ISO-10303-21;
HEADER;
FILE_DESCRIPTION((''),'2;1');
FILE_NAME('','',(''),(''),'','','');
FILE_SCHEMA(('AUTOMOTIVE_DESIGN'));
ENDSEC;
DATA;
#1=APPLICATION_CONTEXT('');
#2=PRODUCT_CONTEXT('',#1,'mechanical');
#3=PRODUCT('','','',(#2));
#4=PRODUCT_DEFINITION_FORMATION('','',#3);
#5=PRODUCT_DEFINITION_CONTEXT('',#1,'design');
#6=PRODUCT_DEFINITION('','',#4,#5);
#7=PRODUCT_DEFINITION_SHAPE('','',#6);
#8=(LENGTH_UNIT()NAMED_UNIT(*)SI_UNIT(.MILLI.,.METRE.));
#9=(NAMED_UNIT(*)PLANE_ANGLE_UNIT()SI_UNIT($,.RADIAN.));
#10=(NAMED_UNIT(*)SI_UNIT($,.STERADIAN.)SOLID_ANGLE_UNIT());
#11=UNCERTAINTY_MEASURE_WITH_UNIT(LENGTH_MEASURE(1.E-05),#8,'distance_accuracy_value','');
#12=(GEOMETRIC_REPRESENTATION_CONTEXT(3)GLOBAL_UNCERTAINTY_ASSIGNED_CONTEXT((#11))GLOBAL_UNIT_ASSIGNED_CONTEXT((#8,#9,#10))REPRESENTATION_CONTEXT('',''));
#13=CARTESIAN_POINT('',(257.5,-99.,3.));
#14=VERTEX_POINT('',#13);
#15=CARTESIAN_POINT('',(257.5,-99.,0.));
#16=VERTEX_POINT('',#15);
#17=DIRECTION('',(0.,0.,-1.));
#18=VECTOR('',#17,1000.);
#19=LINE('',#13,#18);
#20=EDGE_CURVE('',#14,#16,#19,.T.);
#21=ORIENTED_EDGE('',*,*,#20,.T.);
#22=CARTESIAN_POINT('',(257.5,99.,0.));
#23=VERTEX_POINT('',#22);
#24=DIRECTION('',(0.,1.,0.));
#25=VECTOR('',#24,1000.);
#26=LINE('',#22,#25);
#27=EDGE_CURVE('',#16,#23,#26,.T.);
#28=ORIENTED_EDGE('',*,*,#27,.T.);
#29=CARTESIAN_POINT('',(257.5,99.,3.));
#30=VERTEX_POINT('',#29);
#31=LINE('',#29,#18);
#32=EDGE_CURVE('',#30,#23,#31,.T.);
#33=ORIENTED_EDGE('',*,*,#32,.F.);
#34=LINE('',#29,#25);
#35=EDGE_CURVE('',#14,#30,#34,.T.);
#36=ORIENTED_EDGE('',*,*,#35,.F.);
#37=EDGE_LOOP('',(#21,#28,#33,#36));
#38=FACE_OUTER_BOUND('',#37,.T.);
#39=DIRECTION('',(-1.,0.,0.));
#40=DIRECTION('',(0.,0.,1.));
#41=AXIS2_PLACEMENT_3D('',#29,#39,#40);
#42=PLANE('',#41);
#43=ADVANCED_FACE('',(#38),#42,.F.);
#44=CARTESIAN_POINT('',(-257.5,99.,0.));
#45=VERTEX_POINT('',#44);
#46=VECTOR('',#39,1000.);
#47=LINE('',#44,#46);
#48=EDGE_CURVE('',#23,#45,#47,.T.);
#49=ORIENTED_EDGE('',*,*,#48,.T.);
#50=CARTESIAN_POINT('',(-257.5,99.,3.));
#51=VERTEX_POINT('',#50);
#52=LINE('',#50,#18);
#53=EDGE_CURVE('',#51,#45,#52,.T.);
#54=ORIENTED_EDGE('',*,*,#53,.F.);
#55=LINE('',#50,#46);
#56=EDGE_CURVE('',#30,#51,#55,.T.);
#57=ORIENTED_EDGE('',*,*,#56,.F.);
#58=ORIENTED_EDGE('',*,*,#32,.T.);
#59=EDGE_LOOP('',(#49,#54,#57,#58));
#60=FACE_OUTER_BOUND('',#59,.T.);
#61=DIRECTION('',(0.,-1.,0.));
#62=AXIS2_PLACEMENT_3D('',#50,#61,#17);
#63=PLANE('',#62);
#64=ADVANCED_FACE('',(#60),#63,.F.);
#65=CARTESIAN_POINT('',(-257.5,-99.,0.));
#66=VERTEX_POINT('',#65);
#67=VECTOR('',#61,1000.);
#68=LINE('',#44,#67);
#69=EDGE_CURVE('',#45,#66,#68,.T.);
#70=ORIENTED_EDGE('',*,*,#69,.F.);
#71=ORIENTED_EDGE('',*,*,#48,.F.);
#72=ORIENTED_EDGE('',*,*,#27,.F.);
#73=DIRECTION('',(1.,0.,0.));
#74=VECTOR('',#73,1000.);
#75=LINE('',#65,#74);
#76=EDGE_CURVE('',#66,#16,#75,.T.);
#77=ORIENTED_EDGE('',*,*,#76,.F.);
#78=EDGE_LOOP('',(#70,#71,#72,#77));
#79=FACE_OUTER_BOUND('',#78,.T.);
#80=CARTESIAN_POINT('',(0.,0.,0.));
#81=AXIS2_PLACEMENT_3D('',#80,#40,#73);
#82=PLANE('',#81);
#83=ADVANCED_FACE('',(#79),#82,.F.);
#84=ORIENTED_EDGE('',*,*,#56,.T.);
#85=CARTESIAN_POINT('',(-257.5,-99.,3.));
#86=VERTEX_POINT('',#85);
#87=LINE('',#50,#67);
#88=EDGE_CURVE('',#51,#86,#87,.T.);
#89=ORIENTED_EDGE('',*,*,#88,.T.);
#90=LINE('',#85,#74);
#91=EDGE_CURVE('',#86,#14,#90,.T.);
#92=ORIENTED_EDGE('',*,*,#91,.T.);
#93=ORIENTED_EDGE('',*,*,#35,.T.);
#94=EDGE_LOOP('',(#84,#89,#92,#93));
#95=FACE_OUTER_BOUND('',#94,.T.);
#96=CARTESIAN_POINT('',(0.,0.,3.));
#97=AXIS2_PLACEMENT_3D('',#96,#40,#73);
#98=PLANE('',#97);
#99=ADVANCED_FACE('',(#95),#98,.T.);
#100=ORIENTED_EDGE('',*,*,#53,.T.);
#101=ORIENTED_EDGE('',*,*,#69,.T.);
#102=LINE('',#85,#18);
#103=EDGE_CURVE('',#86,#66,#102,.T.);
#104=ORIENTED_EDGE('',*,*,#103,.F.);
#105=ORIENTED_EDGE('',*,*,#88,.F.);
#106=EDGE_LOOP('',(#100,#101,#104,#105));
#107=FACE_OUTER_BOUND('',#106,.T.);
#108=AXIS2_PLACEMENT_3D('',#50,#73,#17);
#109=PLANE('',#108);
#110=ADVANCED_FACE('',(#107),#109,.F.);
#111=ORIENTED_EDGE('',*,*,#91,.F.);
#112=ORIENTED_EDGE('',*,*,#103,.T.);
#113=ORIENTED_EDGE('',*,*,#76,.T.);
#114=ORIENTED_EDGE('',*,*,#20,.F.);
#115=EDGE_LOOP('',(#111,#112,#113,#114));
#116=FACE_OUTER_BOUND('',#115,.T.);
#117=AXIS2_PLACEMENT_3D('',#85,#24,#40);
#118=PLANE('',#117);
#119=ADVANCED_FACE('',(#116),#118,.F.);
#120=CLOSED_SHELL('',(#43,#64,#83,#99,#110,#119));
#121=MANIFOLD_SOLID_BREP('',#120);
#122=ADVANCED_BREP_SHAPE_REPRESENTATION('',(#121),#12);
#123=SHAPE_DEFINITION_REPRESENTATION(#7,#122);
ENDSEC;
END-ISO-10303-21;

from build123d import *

# Parameters (mm, degrees)
SKETCH1_W           = 515
SKETCH1_H           = 198
BOSS_EXTRUDE1_DEPTH = 3


with BuildPart() as part:
    # Sketch1 → Boss-Extrude1 (new body)
    with BuildSketch(Plane.XY):
        Rectangle(SKETCH1_W, SKETCH1_H)
    extrude(amount=BOSS_EXTRUDE1_DEPTH)


solid = part.part
